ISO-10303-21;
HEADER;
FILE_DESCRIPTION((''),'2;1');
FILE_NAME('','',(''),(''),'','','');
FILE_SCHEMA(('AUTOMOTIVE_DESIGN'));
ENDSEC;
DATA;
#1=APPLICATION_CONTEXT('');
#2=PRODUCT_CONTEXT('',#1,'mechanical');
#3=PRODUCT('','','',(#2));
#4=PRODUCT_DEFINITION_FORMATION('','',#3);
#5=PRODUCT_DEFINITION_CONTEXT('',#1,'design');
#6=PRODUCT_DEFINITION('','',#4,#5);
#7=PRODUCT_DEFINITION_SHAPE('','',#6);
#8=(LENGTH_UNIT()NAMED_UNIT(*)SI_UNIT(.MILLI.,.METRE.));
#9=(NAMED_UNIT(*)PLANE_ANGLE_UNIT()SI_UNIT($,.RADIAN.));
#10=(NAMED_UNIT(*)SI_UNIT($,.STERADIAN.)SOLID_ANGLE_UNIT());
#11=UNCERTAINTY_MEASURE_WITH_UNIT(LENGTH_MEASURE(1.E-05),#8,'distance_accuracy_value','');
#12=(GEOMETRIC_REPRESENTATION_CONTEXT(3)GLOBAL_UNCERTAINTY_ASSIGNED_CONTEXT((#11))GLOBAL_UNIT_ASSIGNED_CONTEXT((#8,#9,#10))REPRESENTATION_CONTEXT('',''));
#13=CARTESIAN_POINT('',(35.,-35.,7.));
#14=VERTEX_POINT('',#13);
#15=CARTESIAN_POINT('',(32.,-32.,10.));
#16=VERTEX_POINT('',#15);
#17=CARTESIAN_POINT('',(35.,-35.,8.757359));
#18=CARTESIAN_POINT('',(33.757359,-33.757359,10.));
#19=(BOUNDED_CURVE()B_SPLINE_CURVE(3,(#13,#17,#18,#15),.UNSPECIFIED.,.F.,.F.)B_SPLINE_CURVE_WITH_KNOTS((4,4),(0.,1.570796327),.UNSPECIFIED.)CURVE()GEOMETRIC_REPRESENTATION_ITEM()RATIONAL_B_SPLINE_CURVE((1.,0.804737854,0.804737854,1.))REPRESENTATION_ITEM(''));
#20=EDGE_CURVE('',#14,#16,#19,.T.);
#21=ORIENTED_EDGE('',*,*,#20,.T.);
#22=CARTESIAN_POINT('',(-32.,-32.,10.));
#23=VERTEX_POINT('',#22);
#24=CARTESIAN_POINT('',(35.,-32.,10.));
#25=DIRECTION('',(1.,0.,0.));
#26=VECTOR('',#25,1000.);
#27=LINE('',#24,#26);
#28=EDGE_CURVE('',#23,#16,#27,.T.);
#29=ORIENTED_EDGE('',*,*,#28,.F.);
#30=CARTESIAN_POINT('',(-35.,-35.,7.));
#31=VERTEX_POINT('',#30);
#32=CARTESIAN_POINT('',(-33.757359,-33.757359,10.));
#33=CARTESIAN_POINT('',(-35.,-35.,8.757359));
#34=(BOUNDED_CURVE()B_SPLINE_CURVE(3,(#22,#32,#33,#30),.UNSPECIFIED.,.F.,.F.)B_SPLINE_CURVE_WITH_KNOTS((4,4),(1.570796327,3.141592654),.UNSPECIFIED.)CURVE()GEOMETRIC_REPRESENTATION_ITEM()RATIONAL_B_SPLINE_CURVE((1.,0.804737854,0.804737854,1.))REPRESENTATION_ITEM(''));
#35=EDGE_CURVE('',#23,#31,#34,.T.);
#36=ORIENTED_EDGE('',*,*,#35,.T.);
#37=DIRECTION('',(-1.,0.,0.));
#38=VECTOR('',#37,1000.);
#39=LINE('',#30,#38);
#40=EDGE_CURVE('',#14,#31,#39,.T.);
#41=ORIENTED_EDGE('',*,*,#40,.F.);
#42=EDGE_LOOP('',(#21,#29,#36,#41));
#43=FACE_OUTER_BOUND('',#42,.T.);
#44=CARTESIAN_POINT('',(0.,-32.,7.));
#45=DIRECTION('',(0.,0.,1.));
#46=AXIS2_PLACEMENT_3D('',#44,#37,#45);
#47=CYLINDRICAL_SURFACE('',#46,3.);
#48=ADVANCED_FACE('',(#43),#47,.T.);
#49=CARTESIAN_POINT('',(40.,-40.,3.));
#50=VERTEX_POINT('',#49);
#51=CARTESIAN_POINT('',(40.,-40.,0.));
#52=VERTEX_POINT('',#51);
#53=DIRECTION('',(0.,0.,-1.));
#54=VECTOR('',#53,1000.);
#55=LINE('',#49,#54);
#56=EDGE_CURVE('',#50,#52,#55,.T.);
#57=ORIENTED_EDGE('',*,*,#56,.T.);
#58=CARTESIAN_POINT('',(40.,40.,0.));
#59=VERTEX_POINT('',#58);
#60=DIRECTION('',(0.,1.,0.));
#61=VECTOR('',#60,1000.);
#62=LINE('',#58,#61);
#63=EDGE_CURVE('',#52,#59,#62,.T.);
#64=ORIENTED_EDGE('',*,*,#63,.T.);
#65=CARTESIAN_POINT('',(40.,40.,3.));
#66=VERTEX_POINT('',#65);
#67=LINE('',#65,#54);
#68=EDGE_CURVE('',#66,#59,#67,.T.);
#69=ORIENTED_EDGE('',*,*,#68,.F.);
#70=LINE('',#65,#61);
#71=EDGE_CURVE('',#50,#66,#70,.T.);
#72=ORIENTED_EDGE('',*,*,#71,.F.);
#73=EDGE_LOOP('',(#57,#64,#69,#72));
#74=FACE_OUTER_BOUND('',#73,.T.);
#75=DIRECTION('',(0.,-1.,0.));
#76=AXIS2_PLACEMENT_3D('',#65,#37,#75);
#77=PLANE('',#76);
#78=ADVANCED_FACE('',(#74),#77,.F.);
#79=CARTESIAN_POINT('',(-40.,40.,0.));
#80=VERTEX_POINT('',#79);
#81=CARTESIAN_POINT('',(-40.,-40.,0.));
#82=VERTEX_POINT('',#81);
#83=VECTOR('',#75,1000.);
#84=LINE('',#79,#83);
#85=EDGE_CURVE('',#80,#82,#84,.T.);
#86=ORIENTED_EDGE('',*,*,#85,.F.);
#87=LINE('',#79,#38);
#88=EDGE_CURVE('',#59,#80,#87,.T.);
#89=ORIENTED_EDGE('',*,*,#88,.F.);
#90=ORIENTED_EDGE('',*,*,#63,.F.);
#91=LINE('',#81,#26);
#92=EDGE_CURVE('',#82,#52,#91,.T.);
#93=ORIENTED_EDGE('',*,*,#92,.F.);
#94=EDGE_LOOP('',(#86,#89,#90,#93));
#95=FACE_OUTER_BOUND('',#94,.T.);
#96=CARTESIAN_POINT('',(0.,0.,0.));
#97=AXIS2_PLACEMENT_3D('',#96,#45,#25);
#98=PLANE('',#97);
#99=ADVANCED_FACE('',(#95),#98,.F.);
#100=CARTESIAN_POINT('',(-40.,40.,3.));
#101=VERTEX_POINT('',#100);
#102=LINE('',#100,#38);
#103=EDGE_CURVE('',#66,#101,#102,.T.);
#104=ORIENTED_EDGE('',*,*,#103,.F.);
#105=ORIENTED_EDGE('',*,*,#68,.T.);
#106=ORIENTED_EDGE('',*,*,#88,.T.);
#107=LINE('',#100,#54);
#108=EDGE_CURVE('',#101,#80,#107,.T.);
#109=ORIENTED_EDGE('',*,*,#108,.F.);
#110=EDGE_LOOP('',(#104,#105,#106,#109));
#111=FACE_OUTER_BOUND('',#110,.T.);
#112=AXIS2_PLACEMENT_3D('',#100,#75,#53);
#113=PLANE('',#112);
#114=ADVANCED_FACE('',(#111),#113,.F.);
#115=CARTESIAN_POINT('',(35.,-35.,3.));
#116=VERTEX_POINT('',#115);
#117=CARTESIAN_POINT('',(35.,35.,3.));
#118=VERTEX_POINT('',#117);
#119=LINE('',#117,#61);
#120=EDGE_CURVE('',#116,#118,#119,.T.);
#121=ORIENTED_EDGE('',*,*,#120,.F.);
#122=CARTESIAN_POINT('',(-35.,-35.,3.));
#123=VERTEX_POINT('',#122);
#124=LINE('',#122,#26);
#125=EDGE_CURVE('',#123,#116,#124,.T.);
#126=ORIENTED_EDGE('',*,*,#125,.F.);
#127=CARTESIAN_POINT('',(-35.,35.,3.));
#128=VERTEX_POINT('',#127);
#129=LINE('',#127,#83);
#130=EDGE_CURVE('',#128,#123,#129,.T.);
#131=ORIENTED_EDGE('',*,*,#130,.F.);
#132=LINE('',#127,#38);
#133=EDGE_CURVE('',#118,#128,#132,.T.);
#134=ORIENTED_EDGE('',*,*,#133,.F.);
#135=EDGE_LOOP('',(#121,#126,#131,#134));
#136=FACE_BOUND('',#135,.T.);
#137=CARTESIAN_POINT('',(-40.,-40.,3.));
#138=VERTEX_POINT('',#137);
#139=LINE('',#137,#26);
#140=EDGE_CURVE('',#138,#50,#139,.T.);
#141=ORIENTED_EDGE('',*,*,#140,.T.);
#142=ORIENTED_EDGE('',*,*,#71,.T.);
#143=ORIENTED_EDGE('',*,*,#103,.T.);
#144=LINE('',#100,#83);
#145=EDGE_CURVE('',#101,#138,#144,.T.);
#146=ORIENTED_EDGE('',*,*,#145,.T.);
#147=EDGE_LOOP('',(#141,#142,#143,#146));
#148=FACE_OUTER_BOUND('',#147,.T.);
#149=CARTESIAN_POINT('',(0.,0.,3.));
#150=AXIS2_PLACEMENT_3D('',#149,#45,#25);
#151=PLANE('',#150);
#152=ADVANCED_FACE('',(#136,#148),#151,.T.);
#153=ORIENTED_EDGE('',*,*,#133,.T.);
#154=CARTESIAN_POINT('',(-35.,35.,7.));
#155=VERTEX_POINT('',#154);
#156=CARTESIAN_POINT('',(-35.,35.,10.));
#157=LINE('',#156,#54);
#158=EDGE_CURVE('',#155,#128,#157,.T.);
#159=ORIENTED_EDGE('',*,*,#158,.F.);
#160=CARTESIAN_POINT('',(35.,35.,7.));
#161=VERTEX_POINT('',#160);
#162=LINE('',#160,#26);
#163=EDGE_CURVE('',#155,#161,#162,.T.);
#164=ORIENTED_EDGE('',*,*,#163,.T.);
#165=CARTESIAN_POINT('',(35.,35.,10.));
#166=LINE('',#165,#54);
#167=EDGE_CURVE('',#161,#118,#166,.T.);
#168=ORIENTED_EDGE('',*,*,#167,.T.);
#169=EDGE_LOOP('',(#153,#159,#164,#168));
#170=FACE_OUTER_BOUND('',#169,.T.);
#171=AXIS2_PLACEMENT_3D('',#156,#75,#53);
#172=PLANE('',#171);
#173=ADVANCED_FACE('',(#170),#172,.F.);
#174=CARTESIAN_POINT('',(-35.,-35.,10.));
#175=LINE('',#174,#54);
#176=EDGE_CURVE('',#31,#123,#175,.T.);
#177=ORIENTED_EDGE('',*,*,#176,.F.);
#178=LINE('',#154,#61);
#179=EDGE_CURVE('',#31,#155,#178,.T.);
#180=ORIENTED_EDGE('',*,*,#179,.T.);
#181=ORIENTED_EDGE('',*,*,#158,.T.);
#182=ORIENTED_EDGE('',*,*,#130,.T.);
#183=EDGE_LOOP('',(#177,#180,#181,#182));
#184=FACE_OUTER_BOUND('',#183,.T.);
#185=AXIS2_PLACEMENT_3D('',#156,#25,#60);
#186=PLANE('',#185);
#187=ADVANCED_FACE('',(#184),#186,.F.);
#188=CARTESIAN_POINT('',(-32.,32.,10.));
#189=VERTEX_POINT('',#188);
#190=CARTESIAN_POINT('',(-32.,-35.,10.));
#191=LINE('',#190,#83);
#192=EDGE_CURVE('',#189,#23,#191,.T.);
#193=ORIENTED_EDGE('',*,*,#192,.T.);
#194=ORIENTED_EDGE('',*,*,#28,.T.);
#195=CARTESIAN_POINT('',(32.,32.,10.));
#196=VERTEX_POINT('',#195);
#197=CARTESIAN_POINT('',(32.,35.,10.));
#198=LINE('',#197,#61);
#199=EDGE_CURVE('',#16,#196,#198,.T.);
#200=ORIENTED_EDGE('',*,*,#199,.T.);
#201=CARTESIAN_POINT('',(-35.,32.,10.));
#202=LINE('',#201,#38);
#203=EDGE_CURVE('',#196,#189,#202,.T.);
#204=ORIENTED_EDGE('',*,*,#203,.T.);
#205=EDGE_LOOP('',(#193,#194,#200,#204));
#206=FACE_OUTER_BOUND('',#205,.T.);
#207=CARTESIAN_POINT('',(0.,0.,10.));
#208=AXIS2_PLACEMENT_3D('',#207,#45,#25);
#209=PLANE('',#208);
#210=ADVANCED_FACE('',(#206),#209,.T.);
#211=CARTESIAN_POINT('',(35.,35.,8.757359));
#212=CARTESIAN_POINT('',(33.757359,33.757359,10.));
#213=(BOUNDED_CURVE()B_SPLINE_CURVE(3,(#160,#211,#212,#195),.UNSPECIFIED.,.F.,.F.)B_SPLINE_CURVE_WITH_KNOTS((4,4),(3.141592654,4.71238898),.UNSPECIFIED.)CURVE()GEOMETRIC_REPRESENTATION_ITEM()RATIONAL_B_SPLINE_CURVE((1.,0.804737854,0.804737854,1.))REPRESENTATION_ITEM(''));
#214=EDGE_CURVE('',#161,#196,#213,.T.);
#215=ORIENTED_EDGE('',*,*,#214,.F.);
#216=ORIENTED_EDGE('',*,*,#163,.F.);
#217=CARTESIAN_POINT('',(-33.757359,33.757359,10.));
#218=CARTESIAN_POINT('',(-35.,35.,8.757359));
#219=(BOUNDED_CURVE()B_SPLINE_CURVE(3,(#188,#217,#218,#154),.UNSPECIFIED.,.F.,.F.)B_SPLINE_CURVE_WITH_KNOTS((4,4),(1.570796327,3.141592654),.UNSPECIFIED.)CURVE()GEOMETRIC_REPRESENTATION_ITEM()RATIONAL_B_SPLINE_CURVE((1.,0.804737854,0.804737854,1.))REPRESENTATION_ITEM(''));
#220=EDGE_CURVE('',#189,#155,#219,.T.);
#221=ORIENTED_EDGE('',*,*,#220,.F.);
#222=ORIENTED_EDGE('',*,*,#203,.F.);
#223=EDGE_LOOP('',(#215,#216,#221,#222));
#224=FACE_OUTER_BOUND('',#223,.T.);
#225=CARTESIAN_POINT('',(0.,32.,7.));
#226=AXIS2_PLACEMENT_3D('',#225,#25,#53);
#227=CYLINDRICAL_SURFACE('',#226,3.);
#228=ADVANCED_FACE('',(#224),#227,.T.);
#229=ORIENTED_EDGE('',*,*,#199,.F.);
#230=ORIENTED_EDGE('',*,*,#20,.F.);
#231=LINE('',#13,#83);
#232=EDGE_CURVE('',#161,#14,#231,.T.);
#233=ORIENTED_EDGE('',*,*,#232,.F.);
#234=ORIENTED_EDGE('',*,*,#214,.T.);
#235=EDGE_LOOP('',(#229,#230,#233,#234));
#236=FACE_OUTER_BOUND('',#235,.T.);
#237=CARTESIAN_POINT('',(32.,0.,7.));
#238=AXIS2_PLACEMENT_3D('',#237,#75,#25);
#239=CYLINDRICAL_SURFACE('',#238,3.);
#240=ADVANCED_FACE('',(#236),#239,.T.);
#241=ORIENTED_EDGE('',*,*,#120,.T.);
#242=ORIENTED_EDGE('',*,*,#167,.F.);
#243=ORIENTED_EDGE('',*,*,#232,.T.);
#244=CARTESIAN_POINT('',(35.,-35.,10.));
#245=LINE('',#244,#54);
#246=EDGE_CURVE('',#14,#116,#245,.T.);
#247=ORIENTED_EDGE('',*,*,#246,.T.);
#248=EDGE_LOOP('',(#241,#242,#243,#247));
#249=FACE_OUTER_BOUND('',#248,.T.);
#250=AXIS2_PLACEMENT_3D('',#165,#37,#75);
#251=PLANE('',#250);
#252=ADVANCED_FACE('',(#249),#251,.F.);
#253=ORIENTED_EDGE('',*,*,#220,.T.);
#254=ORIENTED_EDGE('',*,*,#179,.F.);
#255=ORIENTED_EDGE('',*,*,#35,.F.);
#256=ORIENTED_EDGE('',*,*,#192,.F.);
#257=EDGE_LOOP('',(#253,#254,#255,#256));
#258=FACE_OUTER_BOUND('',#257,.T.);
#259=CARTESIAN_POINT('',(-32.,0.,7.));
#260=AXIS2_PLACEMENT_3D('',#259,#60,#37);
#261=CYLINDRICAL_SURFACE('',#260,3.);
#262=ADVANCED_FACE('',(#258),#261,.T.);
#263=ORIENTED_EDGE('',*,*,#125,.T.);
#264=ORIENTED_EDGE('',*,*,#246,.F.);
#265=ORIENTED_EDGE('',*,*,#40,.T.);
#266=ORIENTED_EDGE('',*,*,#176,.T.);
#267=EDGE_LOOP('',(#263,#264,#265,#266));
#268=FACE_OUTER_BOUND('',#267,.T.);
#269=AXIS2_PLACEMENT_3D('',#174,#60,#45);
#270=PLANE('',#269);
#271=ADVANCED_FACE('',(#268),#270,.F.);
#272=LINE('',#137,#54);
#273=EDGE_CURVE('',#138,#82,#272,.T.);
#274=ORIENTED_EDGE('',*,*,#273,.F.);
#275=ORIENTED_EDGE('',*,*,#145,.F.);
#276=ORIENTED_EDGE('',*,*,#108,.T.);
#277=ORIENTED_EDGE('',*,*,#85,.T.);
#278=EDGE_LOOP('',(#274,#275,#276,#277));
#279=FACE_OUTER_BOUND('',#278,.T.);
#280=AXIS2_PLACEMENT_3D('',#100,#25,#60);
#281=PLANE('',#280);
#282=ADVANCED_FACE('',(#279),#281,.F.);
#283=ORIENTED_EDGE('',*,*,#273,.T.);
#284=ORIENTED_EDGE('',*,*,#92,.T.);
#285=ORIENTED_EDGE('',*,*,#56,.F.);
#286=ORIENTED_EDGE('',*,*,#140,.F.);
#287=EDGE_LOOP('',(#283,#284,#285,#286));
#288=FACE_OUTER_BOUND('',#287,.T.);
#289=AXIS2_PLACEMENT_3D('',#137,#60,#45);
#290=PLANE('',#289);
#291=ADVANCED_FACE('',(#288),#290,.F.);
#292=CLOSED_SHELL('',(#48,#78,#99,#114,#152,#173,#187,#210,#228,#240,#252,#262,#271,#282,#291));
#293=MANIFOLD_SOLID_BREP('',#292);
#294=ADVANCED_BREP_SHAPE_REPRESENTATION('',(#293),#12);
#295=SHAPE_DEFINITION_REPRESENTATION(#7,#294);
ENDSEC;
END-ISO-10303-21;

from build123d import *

# Parameters (mm, degrees)
SKETCH1_W           = 80
SKETCH1_H           = 80
BOSS_EXTRUDE1_DEPTH = 3
SKETCH2_W           = 70
SKETCH2_H           = 70
BOSS_EXTRUDE2_DEPTH = 7
FILLET1_R           = 3


with BuildPart() as part:
    # Sketch1 → Boss-Extrude1 (new body)
    with BuildSketch(Plane.XY):
        Rectangle(SKETCH1_W, SKETCH1_H)
    extrude(amount=BOSS_EXTRUDE1_DEPTH)

    # Sketch2 → Boss-Extrude2 (add)
    with BuildSketch(Plane.XY.offset(3)):
        Rectangle(SKETCH2_W, SKETCH2_H)
    extrude(amount=BOSS_EXTRUDE2_DEPTH)

    # Fillet1
    fillet1_edges = [part.edges().sort_by_distance(p)[0] for p in [
        (35, 0, 10),
        (0, 35, 10),
        (-35, 0, 10),
        (0, -35, 10),
    ]]
    fillet(fillet1_edges, radius=FILLET1_R)


solid = part.part
